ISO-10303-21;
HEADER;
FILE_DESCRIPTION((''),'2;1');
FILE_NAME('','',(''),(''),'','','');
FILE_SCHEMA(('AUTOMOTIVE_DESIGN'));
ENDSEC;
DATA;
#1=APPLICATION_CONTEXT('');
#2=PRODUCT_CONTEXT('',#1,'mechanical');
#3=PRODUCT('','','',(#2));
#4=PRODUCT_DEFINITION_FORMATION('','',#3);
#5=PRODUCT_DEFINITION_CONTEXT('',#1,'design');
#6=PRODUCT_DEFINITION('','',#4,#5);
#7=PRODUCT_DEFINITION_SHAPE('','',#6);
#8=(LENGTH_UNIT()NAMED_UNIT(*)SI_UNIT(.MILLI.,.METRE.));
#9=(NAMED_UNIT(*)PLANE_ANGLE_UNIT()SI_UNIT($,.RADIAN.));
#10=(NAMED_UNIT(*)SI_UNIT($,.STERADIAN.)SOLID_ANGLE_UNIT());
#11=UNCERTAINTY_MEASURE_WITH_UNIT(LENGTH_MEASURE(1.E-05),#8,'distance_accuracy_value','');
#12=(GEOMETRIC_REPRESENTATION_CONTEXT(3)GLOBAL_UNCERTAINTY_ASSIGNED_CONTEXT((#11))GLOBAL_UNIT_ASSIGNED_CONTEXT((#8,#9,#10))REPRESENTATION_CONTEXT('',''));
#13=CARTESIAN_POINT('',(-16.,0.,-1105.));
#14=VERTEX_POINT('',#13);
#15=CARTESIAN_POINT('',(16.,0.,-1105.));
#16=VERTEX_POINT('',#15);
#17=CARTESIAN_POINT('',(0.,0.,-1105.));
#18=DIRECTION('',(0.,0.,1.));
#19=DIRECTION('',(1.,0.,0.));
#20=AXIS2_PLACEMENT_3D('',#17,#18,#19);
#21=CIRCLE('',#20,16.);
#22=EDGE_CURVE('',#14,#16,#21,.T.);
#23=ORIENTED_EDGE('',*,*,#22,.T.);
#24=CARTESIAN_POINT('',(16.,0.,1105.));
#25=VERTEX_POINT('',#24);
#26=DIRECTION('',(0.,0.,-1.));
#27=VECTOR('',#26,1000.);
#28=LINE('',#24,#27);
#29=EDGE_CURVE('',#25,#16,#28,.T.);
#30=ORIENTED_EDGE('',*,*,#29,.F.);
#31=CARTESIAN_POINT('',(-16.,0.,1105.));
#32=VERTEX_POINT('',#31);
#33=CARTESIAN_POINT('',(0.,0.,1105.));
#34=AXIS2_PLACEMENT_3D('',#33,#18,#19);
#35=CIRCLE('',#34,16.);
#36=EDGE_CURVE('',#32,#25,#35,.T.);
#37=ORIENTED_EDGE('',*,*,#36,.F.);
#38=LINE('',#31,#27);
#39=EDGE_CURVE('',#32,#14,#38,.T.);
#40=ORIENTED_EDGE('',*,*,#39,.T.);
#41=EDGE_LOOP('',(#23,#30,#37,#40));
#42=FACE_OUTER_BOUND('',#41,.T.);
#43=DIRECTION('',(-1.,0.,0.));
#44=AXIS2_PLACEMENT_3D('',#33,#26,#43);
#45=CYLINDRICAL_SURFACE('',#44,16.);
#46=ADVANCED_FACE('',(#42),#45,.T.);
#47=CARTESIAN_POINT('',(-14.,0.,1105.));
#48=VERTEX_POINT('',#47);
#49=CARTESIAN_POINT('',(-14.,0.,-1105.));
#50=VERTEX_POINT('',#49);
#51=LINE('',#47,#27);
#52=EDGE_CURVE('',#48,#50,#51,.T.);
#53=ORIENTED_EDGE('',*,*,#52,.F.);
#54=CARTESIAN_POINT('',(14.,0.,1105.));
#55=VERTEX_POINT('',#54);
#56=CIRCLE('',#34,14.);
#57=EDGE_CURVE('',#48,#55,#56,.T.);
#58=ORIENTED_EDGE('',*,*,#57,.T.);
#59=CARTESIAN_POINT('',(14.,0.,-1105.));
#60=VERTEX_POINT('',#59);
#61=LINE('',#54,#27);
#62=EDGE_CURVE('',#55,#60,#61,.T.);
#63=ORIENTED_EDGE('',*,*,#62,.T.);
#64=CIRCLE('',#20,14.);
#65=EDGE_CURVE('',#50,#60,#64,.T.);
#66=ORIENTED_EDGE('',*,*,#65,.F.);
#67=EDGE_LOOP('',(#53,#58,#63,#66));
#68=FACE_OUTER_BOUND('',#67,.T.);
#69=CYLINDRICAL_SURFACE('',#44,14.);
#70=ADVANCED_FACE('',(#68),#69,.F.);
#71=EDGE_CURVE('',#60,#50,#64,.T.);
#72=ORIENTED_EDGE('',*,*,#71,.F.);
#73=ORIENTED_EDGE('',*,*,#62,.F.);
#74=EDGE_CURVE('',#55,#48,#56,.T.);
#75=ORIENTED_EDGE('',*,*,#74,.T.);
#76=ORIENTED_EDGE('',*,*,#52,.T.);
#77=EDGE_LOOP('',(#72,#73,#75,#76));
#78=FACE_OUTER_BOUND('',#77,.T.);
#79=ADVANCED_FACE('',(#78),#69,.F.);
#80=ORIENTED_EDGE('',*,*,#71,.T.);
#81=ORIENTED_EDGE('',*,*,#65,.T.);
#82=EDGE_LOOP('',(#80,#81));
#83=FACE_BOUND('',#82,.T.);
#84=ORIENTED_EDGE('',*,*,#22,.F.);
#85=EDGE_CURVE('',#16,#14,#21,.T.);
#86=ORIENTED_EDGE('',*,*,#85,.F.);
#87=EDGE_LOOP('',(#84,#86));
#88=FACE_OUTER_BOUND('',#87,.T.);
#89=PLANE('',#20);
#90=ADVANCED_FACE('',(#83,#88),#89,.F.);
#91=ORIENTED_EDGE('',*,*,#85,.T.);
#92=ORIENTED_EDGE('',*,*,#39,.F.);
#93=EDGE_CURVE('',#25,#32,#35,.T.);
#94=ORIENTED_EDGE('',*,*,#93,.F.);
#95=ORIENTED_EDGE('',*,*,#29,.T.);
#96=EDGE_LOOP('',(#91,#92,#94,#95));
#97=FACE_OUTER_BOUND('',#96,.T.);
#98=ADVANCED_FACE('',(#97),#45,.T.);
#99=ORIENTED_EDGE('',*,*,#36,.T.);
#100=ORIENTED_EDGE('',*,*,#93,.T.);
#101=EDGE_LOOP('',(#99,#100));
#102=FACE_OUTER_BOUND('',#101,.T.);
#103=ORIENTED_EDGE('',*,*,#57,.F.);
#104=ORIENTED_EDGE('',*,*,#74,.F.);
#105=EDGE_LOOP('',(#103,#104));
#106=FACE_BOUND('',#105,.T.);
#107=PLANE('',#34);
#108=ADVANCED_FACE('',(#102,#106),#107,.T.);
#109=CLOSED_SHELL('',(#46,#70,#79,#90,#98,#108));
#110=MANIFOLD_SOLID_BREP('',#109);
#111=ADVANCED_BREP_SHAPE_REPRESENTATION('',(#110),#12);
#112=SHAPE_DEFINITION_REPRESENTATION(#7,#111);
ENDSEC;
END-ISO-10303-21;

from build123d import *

# Parameters (mm, degrees)
SKETCH_1_R      = 16
SKETCH_1_R_2    = 14
EXTRUDE_1_DEPTH = 1105


with BuildPart() as part:
    # 草图1 → 凸台-拉伸1 (new, symmetric)
    with BuildSketch(Plane.XY):
        Circle(SKETCH_1_R)
        Circle(SKETCH_1_R_2, mode=Mode.SUBTRACT)
    extrude(amount=EXTRUDE_1_DEPTH, both=True)


solid = part.part
